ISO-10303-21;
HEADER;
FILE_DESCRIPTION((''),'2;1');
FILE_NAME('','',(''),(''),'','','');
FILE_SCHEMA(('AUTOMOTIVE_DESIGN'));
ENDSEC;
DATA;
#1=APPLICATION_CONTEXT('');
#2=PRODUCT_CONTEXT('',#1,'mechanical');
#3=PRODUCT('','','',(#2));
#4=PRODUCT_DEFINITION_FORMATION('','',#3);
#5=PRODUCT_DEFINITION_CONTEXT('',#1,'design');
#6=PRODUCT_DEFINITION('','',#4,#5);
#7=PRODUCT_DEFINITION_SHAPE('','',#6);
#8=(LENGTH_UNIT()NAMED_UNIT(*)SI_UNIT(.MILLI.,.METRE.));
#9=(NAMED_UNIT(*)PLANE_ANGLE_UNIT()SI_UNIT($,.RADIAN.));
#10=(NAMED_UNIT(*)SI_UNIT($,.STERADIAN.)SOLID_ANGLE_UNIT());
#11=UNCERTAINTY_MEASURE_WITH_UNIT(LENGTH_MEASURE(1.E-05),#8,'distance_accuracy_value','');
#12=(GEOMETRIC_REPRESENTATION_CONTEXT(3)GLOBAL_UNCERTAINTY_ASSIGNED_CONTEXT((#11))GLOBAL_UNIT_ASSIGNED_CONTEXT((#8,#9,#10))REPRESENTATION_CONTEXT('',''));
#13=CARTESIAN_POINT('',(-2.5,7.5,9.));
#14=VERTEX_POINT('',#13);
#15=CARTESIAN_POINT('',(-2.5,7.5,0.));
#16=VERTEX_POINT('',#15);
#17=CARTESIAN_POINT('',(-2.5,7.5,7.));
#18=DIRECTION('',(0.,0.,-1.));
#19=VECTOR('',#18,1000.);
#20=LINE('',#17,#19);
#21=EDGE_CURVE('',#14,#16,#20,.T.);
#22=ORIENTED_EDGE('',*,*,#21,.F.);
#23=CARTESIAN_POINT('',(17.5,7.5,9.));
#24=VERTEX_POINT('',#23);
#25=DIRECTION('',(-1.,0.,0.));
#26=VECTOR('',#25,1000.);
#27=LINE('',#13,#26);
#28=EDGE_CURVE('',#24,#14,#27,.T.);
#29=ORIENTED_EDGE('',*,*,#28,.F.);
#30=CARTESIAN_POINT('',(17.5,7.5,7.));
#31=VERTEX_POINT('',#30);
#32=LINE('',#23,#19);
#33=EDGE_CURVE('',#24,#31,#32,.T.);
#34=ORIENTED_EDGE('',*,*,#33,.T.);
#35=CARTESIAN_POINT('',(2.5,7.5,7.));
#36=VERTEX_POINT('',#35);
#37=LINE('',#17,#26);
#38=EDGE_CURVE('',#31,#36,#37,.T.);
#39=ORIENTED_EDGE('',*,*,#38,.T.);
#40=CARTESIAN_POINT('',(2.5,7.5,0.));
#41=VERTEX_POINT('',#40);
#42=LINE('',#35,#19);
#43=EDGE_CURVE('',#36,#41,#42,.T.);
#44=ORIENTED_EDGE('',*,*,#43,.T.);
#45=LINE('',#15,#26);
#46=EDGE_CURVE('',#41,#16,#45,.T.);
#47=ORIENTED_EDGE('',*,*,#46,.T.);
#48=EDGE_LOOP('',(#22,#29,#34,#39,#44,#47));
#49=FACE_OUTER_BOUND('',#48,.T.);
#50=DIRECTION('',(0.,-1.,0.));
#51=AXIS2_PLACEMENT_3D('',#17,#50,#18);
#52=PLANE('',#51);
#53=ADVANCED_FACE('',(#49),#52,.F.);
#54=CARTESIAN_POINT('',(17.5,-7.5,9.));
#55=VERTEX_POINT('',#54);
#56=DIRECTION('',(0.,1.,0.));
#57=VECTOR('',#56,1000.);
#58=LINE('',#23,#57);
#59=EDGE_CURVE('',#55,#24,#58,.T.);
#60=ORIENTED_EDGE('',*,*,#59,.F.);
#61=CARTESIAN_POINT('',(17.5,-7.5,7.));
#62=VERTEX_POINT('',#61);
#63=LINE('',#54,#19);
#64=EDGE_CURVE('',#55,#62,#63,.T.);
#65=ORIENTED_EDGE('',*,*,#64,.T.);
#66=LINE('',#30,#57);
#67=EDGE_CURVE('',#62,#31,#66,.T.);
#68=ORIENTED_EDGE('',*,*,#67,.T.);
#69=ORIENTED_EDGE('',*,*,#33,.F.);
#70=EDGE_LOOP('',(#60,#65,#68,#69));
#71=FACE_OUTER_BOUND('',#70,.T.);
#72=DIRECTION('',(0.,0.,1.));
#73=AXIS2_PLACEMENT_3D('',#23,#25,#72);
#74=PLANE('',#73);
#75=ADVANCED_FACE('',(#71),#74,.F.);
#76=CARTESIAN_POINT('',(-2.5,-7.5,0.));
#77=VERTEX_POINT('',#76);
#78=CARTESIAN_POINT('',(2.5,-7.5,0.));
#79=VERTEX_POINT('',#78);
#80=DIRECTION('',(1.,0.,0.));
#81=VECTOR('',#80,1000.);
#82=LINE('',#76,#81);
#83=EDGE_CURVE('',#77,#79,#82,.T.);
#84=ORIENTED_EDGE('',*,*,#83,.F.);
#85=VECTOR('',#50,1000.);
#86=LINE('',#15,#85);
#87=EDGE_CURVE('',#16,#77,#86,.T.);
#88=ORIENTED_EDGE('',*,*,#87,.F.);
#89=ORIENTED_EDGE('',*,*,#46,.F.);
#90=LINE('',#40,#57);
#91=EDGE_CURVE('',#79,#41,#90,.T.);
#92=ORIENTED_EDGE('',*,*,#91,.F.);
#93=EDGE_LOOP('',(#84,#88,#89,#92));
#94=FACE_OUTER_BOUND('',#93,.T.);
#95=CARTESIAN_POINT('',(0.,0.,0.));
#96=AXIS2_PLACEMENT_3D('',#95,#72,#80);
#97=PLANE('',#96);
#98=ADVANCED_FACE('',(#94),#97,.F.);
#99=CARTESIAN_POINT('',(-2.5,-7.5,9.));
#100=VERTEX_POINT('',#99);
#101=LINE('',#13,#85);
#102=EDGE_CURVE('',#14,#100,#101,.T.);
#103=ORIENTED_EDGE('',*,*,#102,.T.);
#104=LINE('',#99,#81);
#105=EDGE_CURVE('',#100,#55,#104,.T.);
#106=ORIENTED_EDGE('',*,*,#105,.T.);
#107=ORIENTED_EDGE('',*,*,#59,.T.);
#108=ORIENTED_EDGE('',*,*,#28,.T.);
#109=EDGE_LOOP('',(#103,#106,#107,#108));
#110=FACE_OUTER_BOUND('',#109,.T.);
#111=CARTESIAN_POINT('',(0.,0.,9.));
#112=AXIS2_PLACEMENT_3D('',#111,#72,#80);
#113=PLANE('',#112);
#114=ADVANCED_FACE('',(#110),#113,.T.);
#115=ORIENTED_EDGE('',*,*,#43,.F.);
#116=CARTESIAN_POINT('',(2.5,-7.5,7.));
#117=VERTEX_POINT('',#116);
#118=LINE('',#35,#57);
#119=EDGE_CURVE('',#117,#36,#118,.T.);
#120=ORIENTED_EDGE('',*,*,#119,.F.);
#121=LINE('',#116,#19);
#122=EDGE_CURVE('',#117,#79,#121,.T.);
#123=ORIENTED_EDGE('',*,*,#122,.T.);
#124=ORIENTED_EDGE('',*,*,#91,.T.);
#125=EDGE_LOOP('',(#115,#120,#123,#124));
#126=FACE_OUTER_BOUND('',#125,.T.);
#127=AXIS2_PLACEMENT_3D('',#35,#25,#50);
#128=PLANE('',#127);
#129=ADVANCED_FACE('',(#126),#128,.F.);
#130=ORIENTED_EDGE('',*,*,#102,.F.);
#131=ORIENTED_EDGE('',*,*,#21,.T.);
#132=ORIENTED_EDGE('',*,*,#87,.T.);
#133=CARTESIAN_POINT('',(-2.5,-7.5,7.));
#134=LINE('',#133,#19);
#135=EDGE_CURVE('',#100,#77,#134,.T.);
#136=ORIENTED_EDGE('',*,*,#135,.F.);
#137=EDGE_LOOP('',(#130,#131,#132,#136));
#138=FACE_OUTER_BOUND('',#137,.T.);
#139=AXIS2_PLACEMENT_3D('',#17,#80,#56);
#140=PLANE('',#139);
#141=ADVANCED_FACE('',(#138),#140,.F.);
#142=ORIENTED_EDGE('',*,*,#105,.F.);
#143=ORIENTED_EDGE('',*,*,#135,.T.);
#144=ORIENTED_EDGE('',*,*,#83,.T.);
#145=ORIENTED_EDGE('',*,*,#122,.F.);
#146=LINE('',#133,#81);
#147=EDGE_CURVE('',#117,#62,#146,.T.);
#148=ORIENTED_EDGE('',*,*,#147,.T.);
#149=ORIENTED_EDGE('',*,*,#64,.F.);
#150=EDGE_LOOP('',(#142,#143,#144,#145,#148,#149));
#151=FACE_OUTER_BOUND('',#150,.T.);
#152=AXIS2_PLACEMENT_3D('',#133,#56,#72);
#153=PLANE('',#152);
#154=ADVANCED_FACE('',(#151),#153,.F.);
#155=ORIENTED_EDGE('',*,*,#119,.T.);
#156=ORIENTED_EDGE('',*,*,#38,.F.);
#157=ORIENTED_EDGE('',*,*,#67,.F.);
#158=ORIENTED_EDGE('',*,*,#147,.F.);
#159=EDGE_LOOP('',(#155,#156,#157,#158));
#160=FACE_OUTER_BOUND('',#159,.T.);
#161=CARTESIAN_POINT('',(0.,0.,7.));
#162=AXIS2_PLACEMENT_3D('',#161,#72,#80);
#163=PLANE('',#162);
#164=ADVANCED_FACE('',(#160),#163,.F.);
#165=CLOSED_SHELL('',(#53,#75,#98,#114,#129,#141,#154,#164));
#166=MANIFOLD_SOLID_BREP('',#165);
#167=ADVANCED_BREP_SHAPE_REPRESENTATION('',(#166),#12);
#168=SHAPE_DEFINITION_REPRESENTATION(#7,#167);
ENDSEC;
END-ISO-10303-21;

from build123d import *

# Parameters (mm, degrees)
SKETCH1_W           = 5
SKETCH1_H           = 15
BOSS_EXTRUDE1_DEPTH = 7
SKETCH2_W           = 20
SKETCH2_H           = 15
BOSS_EXTRUDE2_DEPTH = 2


with BuildPart() as part:
    # Sketch1 → Boss-Extrude1 (new body)
    with BuildSketch(Plane.XY):
        Rectangle(SKETCH1_W, SKETCH1_H)
    extrude(amount=BOSS_EXTRUDE1_DEPTH)

    # Sketch2 → Boss-Extrude2 (add)
    with BuildSketch(Plane.XY.offset(7)):
        with Locations((7.5, 0)):
            Rectangle(SKETCH2_W, SKETCH2_H)
    extrude(amount=BOSS_EXTRUDE2_DEPTH)


solid = part.part
